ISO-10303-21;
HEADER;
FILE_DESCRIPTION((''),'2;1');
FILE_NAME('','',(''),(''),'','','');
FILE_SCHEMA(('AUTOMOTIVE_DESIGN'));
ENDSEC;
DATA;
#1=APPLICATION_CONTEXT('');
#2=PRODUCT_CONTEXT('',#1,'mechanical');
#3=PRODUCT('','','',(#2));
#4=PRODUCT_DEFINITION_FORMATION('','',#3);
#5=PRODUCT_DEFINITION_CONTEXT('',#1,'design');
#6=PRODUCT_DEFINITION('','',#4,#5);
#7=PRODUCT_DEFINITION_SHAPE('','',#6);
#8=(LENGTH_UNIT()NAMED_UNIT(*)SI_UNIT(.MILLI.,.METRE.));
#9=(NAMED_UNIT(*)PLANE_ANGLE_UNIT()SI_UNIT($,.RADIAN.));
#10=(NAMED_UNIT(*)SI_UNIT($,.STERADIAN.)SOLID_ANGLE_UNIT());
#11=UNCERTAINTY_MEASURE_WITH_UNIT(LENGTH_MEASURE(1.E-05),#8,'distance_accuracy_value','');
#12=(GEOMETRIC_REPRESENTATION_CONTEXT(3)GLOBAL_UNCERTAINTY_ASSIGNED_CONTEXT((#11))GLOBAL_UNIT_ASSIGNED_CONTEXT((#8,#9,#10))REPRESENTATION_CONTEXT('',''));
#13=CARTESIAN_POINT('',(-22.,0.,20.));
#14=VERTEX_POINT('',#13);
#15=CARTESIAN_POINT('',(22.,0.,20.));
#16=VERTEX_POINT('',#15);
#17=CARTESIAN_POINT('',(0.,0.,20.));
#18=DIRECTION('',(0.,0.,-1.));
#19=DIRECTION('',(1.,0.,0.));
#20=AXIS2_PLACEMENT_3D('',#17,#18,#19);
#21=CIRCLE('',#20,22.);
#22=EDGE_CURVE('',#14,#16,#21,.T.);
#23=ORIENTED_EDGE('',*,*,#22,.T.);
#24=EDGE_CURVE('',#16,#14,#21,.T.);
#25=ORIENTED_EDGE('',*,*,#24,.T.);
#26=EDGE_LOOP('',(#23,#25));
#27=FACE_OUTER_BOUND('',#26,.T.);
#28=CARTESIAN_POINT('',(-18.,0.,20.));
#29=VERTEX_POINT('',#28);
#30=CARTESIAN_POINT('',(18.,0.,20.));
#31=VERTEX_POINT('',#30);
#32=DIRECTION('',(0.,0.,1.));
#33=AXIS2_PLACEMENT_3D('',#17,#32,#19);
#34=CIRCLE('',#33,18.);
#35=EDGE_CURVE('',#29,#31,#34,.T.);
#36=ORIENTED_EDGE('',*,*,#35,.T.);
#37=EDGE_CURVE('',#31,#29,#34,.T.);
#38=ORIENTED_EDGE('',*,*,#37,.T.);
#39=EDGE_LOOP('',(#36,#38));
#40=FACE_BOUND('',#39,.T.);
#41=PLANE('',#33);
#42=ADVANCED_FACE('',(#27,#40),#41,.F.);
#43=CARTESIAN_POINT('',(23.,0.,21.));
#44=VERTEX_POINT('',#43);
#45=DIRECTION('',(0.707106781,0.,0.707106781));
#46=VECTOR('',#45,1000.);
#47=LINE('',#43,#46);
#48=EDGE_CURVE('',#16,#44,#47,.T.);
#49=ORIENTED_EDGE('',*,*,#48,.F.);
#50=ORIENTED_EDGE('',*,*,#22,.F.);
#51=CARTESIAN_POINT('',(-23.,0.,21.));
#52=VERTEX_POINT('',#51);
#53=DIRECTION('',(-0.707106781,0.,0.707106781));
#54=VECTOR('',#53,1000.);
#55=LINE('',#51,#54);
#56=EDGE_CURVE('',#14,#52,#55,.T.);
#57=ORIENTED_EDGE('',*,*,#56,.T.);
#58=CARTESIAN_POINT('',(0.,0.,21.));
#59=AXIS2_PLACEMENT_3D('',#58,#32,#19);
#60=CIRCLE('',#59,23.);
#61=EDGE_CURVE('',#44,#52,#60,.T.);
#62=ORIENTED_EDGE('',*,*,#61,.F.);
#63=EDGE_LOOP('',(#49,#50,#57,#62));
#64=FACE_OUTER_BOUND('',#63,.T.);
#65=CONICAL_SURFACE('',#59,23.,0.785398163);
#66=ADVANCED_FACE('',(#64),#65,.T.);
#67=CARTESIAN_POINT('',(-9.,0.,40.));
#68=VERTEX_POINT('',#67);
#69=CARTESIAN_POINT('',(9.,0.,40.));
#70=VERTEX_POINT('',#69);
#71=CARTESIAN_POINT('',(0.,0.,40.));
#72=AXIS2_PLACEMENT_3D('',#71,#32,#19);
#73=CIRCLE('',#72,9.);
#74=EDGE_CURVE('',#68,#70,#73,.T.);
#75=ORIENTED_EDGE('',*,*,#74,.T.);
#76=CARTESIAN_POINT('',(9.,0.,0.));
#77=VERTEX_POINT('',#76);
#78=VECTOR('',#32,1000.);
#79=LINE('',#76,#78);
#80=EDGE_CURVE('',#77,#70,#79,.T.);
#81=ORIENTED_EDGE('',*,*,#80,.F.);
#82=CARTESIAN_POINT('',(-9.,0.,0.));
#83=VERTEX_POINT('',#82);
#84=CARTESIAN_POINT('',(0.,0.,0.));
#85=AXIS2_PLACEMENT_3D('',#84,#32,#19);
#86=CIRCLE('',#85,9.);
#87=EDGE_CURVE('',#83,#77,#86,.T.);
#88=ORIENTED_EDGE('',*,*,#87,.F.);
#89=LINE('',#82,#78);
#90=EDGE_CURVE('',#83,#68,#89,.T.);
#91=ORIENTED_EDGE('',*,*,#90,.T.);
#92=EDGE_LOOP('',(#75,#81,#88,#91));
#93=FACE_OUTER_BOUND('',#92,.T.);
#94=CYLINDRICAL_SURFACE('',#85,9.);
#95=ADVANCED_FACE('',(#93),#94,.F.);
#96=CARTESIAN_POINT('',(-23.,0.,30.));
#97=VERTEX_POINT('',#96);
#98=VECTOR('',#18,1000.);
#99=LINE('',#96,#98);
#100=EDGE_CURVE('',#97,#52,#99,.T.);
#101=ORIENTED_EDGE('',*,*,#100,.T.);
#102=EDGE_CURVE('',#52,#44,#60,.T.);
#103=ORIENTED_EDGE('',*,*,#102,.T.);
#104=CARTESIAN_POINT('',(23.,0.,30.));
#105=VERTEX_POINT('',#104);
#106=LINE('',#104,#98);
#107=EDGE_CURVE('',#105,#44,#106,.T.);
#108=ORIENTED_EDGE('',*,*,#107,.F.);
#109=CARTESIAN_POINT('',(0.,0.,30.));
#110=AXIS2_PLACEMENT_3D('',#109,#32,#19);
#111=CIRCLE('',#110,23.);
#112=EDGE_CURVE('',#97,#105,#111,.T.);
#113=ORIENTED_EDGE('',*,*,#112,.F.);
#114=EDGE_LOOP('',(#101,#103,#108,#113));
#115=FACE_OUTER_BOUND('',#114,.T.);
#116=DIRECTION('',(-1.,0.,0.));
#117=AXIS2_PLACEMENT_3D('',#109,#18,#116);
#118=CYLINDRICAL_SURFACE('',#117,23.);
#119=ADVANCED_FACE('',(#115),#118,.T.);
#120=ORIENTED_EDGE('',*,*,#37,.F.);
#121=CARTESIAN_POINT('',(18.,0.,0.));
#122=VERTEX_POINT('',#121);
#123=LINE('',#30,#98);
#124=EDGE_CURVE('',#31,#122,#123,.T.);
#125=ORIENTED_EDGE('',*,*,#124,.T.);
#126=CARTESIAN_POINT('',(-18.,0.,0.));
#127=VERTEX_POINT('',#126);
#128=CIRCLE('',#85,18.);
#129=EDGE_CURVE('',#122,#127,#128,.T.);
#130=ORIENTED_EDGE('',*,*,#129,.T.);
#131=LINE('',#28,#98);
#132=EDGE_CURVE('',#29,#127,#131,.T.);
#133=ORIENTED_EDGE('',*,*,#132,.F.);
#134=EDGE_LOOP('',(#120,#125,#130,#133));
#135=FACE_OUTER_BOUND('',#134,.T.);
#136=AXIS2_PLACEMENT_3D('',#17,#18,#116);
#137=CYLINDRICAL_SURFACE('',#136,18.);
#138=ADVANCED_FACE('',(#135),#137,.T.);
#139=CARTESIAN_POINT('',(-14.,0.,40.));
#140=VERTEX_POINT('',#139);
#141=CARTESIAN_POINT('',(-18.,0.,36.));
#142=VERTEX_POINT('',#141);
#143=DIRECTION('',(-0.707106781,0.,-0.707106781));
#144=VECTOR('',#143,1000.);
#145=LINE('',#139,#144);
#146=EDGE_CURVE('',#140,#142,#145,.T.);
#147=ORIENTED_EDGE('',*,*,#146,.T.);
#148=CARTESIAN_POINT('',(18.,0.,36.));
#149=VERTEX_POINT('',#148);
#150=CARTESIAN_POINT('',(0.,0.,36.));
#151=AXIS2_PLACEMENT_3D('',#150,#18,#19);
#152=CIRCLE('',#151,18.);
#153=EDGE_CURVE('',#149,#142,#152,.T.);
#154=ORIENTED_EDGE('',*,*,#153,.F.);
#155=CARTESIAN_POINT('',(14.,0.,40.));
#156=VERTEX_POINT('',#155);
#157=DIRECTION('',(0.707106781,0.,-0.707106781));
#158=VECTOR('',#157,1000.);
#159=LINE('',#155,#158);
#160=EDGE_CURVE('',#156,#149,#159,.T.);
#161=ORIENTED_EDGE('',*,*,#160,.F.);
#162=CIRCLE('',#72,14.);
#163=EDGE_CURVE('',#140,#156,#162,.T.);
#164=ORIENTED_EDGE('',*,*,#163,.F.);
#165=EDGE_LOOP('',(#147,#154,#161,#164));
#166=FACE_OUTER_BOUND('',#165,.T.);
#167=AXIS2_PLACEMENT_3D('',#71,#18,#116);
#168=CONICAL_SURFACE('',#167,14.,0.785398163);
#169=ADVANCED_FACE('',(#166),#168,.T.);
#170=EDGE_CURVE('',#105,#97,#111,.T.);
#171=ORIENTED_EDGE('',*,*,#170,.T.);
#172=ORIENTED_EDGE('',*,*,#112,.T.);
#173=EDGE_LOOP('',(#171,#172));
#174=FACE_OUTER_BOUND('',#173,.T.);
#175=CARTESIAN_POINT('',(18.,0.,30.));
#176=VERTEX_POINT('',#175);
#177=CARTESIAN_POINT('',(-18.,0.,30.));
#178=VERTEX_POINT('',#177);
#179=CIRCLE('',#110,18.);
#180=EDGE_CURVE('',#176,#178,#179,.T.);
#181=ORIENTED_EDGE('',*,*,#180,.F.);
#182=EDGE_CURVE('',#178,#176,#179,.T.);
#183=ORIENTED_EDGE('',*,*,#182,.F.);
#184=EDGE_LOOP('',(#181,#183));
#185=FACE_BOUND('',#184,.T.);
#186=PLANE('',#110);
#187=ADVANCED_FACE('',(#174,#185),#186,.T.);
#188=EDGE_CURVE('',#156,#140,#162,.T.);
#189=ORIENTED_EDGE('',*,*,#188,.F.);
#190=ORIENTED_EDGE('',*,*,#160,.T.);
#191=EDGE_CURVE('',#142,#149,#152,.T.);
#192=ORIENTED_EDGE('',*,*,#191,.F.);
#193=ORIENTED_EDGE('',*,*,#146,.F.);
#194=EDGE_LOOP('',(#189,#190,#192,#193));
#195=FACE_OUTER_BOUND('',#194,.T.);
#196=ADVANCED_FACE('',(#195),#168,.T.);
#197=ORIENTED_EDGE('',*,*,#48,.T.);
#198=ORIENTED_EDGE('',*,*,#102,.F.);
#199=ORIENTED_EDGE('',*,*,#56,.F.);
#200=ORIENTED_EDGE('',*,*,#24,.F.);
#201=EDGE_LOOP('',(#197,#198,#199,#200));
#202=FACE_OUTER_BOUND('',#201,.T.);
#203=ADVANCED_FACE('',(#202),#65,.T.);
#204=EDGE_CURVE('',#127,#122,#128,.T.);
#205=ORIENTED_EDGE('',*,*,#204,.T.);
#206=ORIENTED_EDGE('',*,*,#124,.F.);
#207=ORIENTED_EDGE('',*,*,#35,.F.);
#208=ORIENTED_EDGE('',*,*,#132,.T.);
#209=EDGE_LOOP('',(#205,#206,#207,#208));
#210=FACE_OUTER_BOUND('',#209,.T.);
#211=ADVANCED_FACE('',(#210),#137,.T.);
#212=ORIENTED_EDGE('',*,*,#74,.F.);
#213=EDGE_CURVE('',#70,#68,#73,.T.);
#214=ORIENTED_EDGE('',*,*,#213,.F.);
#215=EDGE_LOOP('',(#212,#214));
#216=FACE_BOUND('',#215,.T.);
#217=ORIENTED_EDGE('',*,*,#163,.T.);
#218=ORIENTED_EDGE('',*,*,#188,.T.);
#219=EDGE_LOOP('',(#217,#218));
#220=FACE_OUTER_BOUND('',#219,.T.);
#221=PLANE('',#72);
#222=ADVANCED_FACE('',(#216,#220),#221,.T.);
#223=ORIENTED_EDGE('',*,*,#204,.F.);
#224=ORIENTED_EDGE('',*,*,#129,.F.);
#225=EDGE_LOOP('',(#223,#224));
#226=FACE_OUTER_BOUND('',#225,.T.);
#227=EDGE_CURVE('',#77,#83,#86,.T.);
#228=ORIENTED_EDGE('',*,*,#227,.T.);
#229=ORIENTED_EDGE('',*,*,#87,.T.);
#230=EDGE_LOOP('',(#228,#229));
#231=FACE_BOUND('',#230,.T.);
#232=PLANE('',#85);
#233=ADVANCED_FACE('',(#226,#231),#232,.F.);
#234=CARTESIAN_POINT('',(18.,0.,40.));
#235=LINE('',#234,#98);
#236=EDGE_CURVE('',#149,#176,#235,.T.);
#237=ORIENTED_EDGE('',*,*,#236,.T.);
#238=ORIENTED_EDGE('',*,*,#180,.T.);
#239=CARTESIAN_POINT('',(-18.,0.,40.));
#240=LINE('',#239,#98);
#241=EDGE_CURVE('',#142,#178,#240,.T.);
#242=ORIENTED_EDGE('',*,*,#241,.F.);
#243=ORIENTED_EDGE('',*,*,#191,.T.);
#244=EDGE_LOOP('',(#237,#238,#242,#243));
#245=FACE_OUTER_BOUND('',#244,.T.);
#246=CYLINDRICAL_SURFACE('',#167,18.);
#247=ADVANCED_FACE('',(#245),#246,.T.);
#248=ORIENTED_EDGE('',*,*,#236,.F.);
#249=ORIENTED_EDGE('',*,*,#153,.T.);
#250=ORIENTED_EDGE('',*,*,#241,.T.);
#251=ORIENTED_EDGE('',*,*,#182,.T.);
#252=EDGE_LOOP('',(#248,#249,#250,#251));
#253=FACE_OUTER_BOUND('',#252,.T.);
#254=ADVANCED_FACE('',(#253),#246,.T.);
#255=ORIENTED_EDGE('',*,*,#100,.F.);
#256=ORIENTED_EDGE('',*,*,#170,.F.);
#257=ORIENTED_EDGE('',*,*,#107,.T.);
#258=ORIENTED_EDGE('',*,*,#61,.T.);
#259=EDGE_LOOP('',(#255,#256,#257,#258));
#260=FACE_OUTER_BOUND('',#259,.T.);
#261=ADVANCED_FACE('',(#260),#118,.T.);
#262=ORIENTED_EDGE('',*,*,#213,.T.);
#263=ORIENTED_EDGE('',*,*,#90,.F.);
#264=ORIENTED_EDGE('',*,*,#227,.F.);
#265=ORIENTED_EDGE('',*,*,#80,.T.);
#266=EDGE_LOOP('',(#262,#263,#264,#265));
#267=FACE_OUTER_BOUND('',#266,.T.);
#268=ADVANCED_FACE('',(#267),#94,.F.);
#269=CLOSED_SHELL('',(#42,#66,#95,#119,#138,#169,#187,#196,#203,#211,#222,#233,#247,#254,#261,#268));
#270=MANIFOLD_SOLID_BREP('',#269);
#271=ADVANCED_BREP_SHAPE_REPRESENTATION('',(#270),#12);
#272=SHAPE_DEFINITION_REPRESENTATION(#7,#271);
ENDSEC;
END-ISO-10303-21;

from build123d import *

# Parameters (mm, degrees)
SKETCH1_R           = 18
BOSS_EXTRUDE1_DEPTH = 20
SKETCH2_R           = 23
BOSS_EXTRUDE2_DEPTH = 10
SKETCH3_R           = 18
BOSS_EXTRUDE3_DEPTH = 10
CHAMFER1_SIZE       = 4
SKETCH4_R           = 9
CUT_EXTRUDE1_DEPTH  = 52.555795019
CHAMFER2_SIZE       = 1


with BuildPart() as part:
    # Sketch1 → Boss-Extrude1 (new body)
    with BuildSketch(Plane.XY):
        Circle(SKETCH1_R)
    extrude(amount=BOSS_EXTRUDE1_DEPTH)

    # Sketch2 → Boss-Extrude2 (add)
    with BuildSketch(Plane.XY.offset(20)):
        Circle(SKETCH2_R)
    extrude(amount=BOSS_EXTRUDE2_DEPTH)

    # Sketch3 → Boss-Extrude3 (add)
    with BuildSketch(Plane.XY.offset(30)):
        Circle(SKETCH3_R)
    extrude(amount=BOSS_EXTRUDE3_DEPTH)

    # Chamfer1
    chamfer1_edges = [part.edges().sort_by_distance(p)[0] for p in [
        (-18, 0, 40),
    ]]
    chamfer(chamfer1_edges, length=CHAMFER1_SIZE)

    # Sketch4 → Cut-Extrude1 (cut, through all)
    with BuildSketch(Plane.XY.offset(40)):
        Circle(SKETCH4_R)
    extrude(amount=-CUT_EXTRUDE1_DEPTH, mode=Mode.SUBTRACT)

    # Chamfer2
    chamfer2_edges = [part.edges().sort_by_distance(p)[0] for p in [
        (-23, 0, 20),
    ]]
    chamfer(chamfer2_edges, length=CHAMFER2_SIZE)


solid = part.part
